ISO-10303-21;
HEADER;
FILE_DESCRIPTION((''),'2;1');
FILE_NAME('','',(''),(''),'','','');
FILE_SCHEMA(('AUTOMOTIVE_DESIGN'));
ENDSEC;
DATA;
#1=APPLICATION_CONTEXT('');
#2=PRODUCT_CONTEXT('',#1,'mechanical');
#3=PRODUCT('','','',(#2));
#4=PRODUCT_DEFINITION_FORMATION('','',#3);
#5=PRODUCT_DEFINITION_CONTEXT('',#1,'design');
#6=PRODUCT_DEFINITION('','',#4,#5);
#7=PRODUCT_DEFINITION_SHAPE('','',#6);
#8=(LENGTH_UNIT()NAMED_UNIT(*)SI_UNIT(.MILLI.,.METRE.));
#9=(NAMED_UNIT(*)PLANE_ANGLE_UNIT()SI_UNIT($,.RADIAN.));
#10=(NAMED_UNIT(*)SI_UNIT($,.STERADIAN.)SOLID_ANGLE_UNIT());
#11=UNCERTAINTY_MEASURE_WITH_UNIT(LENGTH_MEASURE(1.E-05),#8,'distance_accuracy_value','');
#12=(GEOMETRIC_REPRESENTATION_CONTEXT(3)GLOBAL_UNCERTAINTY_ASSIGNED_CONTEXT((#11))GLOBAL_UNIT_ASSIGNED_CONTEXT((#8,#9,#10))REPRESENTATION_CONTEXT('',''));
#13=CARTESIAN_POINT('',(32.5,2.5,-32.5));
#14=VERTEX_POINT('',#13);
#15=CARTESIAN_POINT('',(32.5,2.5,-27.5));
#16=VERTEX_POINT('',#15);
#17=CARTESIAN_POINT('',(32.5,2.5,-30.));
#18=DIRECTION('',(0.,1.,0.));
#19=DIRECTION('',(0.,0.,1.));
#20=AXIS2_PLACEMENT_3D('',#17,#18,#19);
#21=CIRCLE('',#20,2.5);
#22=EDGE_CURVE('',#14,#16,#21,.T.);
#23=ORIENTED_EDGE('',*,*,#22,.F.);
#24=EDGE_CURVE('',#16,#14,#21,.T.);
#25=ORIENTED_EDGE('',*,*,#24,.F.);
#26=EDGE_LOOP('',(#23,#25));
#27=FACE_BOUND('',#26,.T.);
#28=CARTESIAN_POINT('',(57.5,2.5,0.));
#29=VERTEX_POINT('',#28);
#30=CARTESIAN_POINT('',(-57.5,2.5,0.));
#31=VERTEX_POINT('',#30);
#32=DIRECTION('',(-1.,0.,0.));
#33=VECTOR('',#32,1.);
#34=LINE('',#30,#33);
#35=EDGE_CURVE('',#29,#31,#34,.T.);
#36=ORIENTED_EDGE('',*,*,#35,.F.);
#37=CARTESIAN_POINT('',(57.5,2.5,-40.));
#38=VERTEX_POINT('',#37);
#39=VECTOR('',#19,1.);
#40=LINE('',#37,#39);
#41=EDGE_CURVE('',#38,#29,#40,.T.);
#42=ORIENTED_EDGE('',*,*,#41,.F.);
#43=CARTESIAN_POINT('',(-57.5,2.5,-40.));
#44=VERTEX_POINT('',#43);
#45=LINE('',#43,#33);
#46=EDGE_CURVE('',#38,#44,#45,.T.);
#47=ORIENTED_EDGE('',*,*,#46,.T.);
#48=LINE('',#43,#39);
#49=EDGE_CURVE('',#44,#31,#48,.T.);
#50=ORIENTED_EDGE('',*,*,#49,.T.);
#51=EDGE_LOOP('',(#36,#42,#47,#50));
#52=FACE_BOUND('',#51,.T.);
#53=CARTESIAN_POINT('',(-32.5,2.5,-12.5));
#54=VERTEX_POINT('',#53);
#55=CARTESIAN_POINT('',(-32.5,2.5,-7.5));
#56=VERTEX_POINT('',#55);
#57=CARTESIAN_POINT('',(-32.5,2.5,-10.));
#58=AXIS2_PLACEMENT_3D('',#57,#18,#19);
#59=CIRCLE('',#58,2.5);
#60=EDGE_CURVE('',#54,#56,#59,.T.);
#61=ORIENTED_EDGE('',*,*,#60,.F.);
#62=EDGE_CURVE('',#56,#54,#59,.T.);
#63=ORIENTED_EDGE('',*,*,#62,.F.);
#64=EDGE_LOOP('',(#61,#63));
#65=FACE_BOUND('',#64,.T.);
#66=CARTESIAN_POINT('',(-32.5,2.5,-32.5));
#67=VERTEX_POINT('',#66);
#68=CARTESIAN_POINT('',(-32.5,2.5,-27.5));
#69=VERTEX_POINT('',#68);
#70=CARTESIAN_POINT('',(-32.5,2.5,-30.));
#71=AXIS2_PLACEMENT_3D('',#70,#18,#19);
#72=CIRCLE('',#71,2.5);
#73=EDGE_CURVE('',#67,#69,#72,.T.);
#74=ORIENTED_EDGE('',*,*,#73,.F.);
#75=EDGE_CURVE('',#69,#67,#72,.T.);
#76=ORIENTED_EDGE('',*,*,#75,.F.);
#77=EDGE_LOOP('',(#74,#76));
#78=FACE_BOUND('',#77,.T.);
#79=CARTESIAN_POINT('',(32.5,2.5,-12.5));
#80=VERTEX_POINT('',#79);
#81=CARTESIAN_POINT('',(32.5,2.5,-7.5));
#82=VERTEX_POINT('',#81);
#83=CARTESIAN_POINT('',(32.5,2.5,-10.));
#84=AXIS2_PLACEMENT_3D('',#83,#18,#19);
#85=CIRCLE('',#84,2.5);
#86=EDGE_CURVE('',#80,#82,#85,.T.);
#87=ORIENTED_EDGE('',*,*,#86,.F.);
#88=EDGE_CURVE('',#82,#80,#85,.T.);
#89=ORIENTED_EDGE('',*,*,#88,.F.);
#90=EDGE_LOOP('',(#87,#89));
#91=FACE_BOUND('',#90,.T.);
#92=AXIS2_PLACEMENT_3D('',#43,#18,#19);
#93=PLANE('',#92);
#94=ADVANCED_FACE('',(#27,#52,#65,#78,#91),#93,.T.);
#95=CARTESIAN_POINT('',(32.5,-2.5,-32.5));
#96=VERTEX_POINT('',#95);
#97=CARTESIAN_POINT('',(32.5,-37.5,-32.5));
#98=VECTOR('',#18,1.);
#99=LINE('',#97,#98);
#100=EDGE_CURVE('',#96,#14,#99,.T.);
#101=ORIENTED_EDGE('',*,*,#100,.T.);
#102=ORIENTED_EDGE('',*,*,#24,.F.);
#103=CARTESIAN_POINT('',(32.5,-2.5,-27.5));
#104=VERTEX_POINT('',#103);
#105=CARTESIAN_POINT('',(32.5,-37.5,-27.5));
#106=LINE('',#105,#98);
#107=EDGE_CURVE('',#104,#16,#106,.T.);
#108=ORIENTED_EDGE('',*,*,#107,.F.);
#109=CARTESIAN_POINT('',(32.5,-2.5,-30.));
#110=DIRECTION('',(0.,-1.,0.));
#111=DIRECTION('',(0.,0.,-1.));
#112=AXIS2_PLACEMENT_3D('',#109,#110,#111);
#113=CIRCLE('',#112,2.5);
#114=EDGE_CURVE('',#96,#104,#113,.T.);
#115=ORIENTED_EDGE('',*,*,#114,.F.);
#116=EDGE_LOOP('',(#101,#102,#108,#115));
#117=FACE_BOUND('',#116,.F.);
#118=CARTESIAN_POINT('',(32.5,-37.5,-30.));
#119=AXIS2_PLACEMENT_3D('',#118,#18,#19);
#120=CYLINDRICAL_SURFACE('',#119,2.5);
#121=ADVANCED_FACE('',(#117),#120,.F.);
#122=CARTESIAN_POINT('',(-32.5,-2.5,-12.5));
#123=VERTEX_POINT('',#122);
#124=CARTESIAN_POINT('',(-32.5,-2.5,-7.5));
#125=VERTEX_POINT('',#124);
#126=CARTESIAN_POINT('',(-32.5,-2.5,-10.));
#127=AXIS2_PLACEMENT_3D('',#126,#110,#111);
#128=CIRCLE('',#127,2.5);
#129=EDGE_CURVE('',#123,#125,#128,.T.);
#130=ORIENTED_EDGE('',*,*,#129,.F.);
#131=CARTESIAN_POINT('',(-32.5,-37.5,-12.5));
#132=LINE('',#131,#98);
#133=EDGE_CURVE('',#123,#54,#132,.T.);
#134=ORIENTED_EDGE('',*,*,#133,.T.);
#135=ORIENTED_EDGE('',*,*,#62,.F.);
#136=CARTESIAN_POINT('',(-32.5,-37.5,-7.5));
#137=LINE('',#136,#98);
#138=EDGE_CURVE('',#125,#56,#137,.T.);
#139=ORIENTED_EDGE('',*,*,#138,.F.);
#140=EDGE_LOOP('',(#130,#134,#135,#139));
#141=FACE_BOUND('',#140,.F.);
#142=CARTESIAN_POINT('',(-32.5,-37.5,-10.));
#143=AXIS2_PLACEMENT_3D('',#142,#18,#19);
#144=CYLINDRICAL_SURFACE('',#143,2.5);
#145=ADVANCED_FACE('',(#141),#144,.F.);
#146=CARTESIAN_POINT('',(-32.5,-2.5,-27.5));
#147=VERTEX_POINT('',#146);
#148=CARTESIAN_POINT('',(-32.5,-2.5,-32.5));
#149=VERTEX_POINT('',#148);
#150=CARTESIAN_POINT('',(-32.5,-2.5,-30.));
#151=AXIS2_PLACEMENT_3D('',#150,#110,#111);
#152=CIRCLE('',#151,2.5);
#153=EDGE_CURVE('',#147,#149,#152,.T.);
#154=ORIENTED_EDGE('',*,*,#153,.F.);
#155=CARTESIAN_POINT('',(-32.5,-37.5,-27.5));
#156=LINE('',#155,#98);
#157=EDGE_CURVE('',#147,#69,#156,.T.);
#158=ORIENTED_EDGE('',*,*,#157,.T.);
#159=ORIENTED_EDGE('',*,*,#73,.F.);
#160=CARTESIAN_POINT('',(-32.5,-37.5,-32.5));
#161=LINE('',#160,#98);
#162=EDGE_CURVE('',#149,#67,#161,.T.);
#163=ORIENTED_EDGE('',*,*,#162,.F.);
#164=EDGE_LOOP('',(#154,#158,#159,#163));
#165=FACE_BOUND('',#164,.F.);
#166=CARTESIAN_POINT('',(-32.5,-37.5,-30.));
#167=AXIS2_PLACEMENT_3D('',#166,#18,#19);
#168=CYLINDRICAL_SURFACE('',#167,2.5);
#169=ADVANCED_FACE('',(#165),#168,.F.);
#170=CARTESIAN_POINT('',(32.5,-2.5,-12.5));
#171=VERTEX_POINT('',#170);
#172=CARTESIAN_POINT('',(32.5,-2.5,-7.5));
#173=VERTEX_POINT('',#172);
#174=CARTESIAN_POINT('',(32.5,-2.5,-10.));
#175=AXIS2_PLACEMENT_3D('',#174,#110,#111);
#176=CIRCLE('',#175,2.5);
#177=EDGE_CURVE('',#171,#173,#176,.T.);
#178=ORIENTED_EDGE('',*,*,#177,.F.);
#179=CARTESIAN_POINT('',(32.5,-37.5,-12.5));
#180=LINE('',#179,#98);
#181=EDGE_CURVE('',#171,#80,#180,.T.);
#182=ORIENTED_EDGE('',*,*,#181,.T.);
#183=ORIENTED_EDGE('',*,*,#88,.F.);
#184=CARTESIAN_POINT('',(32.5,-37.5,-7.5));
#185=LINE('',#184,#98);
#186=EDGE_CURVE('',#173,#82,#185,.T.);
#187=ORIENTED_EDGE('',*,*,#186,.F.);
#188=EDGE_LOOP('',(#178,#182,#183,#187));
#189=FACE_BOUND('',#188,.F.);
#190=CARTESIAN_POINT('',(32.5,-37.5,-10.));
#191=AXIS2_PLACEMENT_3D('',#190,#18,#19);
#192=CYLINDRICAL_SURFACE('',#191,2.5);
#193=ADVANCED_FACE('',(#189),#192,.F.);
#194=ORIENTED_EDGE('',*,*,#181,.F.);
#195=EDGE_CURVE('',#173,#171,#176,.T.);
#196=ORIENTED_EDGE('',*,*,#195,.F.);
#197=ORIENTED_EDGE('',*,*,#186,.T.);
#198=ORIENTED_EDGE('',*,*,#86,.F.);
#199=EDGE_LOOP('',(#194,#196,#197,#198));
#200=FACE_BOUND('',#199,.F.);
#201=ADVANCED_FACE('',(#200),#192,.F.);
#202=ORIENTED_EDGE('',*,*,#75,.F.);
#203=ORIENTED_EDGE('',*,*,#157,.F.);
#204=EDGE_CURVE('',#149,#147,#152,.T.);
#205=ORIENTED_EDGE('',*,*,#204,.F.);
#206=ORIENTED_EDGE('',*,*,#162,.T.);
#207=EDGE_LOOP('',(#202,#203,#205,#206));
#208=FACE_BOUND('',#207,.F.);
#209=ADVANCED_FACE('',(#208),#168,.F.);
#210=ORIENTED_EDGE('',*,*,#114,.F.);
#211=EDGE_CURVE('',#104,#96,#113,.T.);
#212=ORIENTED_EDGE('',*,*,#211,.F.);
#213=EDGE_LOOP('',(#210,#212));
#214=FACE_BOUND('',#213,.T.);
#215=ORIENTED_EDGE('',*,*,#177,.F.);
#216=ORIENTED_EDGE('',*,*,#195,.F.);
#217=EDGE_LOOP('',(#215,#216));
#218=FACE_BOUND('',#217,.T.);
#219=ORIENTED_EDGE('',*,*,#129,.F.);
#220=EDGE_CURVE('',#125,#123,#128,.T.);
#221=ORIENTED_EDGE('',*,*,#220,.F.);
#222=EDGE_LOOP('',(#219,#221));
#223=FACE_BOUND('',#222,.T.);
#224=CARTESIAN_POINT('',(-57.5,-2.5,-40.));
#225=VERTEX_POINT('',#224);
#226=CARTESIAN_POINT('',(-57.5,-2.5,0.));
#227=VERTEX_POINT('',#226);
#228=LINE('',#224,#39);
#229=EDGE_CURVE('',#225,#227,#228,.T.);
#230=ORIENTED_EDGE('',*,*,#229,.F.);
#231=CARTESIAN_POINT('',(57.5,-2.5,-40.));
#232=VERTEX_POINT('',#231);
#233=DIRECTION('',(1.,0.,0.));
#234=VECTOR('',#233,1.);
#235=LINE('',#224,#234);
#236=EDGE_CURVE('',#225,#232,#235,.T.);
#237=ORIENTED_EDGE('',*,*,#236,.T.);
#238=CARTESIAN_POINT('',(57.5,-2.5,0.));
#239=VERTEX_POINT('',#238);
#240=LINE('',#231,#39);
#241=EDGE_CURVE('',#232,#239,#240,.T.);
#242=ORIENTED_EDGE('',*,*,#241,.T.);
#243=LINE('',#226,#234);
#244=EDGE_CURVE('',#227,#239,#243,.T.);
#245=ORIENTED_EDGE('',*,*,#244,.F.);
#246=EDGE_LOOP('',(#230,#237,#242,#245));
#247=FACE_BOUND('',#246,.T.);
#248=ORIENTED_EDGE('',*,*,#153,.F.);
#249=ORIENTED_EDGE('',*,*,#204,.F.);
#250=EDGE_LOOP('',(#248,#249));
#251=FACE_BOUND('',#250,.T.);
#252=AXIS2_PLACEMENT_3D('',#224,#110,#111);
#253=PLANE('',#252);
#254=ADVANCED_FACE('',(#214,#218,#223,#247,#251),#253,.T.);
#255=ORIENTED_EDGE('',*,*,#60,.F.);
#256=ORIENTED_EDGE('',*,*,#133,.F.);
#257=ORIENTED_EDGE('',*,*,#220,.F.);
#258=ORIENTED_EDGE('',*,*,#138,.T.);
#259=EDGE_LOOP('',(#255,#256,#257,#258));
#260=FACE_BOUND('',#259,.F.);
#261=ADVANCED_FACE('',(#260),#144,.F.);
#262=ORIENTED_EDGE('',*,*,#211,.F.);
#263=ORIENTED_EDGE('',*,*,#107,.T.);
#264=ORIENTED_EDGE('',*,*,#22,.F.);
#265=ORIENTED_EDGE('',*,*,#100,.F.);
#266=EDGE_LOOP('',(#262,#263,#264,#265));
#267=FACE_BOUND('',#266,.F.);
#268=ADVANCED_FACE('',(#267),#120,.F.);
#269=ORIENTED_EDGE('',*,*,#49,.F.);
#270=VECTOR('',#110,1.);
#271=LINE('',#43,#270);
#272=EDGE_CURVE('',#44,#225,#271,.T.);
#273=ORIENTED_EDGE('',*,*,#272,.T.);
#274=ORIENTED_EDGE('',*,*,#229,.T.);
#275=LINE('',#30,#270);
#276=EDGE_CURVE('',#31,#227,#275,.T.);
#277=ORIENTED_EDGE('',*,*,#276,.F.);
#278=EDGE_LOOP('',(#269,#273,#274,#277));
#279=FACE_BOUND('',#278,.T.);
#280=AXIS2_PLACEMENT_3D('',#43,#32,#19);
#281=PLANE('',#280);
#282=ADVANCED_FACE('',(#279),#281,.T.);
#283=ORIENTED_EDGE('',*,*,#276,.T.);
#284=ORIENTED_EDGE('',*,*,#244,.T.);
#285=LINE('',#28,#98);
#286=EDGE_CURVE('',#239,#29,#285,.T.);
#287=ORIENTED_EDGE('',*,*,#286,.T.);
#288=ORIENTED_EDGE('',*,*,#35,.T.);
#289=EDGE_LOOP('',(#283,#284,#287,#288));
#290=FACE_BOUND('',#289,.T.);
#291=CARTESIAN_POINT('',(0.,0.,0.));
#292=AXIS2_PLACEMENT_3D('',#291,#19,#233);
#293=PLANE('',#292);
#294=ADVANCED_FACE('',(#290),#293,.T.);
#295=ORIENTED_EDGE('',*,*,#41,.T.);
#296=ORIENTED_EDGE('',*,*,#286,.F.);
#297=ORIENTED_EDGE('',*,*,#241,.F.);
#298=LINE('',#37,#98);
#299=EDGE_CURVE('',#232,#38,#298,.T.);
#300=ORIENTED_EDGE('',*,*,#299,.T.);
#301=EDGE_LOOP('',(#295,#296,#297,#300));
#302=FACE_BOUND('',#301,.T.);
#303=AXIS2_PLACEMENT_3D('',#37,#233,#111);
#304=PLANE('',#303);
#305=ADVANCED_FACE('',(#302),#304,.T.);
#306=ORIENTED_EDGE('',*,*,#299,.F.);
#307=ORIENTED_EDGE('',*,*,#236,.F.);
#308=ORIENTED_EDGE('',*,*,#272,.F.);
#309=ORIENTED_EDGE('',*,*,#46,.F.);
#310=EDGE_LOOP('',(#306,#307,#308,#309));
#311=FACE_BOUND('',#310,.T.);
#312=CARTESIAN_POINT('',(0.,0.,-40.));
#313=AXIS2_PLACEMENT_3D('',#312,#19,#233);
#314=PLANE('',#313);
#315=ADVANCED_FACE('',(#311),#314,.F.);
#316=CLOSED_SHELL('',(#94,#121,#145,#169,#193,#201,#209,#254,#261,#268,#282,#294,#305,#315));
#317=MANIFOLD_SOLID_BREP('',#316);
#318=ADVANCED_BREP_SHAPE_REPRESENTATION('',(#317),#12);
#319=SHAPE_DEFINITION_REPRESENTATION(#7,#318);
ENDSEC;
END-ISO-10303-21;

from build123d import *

# Parameters (mm, degrees)
SKETCH1_W           = 115
SKETCH1_H           = 5
BOSS_EXTRUDE1_DEPTH = 40
SKETCH2_R           = 2.5
CUT_EXTRUDE1_DEPTH  = 40


with BuildPart() as part:
    # Sketch1 → Boss-Extrude1 (new body)
    with BuildSketch(Plane.XY):
        Rectangle(SKETCH1_W, SKETCH1_H)
    extrude(amount=-BOSS_EXTRUDE1_DEPTH)

    # Sketch2 → Cut-Extrude1 (cut)
    with BuildSketch(Plane(origin=(0, 2.5, 0), x_dir=(1, 0, 0), z_dir=(0, 1, 0))):
        with Locations(Location((-32.5, 30, 0), (0, 0, 270))):
            Circle(SKETCH2_R)
        with Locations(Location((32.5, 30, 0), (0, 0, 270))):
            Circle(SKETCH2_R)
        with Locations(Location((-32.5, 10, 0), (0, 0, 270))):
            Circle(SKETCH2_R)
        with Locations(Location((32.5, 10, 0), (0, 0, 270))):
            Circle(SKETCH2_R)
    extrude(amount=-CUT_EXTRUDE1_DEPTH, mode=Mode.SUBTRACT)


solid = part.part
